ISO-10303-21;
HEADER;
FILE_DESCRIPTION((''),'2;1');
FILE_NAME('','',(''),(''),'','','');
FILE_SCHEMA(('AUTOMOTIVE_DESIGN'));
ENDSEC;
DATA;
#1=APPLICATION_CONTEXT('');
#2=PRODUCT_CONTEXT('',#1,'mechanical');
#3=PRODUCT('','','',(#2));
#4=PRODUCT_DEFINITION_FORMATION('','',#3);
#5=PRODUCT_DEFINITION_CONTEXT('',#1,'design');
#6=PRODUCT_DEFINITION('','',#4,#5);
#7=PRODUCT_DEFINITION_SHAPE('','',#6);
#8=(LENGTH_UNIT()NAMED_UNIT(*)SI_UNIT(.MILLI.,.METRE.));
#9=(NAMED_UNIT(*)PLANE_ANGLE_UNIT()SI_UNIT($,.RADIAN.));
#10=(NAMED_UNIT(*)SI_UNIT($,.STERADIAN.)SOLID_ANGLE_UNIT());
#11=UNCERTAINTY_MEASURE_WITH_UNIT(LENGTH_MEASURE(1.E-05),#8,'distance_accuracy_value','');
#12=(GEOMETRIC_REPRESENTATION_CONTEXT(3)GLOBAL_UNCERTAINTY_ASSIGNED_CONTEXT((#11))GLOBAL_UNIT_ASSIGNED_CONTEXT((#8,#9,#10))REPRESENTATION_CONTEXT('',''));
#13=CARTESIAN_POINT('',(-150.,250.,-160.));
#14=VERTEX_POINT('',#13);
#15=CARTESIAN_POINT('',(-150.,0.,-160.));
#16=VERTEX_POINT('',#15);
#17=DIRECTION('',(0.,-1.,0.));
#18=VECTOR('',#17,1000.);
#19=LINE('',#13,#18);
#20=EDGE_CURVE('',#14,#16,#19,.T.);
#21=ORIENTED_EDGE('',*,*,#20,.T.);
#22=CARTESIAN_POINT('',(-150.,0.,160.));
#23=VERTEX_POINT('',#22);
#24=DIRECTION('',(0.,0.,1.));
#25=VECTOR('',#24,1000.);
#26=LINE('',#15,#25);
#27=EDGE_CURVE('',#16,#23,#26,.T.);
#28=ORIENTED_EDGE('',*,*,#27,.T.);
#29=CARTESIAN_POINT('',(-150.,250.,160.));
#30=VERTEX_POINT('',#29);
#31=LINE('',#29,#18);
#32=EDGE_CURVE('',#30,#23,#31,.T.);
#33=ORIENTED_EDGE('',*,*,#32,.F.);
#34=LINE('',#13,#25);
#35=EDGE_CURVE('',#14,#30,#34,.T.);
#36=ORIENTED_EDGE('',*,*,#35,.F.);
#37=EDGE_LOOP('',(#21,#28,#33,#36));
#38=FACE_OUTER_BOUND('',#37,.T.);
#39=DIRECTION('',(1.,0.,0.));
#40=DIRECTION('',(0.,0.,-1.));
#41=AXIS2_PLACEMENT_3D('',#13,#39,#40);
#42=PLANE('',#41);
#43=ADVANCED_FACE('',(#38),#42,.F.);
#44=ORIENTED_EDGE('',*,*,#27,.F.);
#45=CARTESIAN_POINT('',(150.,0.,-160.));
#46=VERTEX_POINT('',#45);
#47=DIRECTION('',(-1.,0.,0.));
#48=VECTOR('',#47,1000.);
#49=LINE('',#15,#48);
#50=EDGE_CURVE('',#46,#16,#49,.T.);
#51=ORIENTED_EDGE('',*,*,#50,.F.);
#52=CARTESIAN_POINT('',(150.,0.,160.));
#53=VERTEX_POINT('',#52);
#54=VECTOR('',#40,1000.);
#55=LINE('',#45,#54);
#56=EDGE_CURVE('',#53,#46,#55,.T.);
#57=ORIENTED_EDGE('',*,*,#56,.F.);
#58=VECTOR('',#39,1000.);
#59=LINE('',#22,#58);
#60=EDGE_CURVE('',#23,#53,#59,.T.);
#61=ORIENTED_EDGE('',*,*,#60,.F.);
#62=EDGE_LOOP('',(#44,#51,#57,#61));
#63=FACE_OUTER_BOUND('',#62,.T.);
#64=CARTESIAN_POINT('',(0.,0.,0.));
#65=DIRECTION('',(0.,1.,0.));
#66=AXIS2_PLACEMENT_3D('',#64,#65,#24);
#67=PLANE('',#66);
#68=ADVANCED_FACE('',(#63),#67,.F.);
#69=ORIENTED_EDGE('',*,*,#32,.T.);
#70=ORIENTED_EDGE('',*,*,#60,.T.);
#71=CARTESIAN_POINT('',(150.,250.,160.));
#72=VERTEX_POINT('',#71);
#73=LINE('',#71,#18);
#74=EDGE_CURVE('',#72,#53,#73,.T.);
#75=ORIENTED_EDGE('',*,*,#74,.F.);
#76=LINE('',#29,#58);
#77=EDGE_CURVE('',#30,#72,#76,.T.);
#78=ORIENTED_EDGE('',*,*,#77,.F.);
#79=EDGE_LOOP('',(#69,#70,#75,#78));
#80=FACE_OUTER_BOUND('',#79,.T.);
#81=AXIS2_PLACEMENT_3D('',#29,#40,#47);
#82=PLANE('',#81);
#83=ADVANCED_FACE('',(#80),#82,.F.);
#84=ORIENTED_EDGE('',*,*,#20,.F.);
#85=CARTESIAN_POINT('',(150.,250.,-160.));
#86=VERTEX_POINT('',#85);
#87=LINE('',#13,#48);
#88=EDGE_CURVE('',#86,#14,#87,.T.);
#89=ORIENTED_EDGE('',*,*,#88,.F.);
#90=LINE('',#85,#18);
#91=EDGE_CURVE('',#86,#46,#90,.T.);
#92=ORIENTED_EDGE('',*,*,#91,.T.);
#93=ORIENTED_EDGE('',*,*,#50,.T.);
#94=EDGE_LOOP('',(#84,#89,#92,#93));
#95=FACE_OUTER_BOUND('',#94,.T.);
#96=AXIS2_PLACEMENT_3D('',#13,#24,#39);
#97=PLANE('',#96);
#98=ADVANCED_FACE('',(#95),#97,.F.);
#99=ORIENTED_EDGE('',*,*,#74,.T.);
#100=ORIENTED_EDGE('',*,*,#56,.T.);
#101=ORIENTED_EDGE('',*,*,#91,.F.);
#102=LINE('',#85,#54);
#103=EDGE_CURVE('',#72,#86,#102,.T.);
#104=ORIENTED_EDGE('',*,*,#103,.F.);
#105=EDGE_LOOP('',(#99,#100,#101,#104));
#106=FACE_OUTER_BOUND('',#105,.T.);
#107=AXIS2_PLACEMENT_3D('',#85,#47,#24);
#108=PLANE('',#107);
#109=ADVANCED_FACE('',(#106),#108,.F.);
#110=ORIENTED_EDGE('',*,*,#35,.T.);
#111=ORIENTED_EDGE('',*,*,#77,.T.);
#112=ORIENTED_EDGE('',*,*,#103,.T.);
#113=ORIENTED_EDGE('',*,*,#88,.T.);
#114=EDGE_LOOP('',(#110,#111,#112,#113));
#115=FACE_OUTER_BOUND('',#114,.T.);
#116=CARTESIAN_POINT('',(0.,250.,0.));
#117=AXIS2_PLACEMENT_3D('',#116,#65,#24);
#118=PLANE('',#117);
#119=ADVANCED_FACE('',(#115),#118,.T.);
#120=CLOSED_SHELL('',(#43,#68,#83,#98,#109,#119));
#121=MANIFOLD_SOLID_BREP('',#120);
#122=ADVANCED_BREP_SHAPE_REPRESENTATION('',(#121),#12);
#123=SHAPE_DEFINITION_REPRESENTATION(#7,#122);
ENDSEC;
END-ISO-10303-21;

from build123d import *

# Parameters (mm, degrees)
SKETCH1_W           = 300
SKETCH1_H           = 320
BOSS_EXTRUDE1_DEPTH = 250


with BuildPart() as part:
    # Sketch1 → Boss-Extrude1 (new body)
    with BuildSketch(Plane(origin=(0, 0, 0), x_dir=(1, 0, 0), z_dir=(0, 1, 0))):
        Rectangle(SKETCH1_W, SKETCH1_H)
    extrude(amount=BOSS_EXTRUDE1_DEPTH)


solid = part.part
